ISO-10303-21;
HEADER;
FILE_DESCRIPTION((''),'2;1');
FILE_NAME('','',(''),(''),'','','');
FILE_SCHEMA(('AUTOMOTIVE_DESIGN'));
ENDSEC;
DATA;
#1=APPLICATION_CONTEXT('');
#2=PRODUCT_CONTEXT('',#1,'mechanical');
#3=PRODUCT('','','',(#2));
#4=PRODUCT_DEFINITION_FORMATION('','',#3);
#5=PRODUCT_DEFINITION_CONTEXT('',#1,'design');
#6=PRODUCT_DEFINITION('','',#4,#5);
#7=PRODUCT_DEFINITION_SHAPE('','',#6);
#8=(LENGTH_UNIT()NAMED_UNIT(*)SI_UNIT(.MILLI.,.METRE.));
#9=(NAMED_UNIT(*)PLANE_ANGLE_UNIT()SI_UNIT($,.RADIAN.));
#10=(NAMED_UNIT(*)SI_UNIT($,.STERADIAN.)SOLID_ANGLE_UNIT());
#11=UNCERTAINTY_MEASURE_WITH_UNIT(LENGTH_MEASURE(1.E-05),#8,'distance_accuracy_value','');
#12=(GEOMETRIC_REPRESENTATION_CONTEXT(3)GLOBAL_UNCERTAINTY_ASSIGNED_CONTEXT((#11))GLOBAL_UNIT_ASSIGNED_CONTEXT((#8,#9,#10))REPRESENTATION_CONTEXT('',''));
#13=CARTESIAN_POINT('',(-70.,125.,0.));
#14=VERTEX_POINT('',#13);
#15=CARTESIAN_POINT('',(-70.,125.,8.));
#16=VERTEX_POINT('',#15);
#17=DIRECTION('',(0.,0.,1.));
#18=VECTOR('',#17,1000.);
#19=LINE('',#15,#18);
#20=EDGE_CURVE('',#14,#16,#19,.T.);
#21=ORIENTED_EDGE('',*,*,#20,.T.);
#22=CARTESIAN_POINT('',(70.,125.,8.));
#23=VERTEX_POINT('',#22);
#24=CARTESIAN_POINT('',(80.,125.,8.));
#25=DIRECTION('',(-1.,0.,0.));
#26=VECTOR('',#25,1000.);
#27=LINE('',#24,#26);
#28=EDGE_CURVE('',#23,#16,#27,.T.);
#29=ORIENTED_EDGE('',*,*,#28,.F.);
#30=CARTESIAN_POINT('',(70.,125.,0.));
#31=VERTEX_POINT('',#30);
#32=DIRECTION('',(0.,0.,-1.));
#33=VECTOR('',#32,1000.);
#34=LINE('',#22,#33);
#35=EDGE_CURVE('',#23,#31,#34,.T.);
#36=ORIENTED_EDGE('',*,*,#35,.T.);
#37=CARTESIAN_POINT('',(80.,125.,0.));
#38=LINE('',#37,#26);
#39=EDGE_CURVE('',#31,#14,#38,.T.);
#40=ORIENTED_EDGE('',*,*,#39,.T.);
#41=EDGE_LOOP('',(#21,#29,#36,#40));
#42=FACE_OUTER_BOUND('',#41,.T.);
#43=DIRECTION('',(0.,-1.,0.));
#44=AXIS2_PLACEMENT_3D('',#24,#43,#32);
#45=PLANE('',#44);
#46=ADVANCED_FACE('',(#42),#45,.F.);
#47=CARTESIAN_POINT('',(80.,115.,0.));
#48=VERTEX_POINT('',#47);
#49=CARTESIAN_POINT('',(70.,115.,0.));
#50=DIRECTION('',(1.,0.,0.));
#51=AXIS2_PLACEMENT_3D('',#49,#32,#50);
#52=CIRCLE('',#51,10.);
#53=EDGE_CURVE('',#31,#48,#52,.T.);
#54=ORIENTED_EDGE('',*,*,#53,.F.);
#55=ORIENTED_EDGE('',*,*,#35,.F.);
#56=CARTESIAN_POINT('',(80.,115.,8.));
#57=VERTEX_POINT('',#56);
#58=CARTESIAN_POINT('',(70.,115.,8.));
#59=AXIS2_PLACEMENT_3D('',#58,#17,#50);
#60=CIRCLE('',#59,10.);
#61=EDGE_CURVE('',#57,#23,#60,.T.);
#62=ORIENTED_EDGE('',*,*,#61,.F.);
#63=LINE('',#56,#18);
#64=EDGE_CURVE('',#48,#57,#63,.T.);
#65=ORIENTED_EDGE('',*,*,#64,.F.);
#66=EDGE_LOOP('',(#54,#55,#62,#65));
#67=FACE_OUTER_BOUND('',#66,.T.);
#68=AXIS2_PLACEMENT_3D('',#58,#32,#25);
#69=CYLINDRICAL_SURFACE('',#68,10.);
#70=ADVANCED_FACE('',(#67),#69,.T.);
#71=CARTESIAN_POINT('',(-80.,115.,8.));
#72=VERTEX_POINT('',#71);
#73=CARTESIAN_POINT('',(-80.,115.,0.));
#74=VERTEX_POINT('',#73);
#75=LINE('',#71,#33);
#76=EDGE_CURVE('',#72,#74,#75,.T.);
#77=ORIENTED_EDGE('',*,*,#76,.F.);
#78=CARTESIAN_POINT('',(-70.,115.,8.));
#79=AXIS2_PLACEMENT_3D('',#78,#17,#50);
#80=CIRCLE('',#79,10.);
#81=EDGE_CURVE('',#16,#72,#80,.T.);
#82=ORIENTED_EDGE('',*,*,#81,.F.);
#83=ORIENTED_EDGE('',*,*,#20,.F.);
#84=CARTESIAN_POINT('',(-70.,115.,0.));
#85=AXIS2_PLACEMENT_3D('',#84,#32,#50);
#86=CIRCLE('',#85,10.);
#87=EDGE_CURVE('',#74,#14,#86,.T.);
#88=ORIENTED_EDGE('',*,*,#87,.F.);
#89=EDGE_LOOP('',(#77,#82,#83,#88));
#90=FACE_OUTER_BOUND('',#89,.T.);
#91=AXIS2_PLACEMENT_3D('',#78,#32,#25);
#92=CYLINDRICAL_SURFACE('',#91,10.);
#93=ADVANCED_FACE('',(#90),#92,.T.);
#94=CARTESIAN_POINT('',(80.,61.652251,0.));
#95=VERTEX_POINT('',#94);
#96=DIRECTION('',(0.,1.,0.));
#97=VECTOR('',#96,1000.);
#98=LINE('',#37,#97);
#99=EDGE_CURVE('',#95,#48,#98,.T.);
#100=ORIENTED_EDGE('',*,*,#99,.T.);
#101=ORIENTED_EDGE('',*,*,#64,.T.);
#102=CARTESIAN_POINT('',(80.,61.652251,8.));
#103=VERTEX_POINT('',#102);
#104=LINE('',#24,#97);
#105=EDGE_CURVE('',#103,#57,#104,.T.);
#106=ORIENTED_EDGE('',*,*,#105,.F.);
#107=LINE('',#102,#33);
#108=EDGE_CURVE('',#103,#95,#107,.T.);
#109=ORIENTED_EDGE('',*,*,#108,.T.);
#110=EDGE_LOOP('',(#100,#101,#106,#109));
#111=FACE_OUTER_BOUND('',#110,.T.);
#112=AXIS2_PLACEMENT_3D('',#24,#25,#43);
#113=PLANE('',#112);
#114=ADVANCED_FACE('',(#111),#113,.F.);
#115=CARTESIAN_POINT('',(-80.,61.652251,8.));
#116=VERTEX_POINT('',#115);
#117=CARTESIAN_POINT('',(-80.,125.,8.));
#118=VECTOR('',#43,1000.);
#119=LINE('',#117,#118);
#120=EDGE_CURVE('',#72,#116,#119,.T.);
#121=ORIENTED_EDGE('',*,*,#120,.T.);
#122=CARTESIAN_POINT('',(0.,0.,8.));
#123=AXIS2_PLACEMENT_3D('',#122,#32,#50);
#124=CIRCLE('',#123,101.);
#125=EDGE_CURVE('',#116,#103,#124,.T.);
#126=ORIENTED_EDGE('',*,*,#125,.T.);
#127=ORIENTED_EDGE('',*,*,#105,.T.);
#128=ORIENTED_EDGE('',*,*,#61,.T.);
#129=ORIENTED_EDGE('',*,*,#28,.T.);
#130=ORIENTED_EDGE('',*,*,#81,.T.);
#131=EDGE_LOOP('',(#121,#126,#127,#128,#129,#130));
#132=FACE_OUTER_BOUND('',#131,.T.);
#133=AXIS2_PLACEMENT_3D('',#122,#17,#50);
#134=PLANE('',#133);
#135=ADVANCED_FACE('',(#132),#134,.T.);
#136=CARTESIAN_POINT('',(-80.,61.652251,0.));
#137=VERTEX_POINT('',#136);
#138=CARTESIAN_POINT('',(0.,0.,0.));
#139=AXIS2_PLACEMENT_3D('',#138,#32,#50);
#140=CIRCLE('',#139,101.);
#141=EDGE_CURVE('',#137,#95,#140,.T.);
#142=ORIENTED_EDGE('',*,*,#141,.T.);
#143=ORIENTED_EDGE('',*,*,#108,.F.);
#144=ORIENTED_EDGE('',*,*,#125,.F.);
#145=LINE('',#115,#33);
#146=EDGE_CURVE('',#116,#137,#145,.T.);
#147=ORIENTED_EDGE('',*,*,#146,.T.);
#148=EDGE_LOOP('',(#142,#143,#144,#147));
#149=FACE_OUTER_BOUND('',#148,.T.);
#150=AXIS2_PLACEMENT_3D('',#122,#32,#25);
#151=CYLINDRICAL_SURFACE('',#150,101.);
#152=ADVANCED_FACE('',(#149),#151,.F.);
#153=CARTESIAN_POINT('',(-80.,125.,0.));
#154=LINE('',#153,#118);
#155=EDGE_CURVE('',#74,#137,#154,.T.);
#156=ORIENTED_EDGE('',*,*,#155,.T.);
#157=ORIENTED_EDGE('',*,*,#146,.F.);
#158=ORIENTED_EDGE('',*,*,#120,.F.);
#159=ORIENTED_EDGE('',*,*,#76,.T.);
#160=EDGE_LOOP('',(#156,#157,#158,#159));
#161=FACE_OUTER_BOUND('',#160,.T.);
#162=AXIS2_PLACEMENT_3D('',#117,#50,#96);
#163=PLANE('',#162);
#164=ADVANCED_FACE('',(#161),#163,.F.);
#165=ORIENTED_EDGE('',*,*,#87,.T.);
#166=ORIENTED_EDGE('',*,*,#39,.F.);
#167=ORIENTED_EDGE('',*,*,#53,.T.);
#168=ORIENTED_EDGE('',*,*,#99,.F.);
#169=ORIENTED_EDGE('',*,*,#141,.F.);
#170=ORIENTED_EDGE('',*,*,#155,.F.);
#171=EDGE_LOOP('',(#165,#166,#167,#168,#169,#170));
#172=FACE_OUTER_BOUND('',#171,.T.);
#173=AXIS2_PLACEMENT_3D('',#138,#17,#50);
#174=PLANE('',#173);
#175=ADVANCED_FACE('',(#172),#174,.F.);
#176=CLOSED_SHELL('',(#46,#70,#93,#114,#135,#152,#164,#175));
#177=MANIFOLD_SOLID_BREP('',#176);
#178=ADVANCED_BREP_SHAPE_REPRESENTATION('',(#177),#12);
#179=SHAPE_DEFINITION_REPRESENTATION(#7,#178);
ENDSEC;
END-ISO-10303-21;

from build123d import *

# Parameters (mm, degrees)
BOSS_EXTRUDE1_DEPTH = 8
FILLET1_R           = 10


with BuildPart() as part:
    # Sketch1 → Boss-Extrude1 (new body)
    with BuildSketch(Plane.XY):
        with BuildLine():
            Line((80, 125), (-80, 125))
            Line((-80, 125), (-80, 61.652250567))
            ThreePointArc((-80, 61.652250567), (0, 101), (80, 61.652250567))
            Line((80, 61.652250567), (80, 125))
        make_face()
    extrude(amount=BOSS_EXTRUDE1_DEPTH)

    # Fillet1
    fillet1_edges = [part.edges().sort_by_distance(p)[0] for p in [
        (-80, 125, 4),
        (80, 125, 4),
    ]]
    fillet(fillet1_edges, radius=FILLET1_R)


solid = part.part
